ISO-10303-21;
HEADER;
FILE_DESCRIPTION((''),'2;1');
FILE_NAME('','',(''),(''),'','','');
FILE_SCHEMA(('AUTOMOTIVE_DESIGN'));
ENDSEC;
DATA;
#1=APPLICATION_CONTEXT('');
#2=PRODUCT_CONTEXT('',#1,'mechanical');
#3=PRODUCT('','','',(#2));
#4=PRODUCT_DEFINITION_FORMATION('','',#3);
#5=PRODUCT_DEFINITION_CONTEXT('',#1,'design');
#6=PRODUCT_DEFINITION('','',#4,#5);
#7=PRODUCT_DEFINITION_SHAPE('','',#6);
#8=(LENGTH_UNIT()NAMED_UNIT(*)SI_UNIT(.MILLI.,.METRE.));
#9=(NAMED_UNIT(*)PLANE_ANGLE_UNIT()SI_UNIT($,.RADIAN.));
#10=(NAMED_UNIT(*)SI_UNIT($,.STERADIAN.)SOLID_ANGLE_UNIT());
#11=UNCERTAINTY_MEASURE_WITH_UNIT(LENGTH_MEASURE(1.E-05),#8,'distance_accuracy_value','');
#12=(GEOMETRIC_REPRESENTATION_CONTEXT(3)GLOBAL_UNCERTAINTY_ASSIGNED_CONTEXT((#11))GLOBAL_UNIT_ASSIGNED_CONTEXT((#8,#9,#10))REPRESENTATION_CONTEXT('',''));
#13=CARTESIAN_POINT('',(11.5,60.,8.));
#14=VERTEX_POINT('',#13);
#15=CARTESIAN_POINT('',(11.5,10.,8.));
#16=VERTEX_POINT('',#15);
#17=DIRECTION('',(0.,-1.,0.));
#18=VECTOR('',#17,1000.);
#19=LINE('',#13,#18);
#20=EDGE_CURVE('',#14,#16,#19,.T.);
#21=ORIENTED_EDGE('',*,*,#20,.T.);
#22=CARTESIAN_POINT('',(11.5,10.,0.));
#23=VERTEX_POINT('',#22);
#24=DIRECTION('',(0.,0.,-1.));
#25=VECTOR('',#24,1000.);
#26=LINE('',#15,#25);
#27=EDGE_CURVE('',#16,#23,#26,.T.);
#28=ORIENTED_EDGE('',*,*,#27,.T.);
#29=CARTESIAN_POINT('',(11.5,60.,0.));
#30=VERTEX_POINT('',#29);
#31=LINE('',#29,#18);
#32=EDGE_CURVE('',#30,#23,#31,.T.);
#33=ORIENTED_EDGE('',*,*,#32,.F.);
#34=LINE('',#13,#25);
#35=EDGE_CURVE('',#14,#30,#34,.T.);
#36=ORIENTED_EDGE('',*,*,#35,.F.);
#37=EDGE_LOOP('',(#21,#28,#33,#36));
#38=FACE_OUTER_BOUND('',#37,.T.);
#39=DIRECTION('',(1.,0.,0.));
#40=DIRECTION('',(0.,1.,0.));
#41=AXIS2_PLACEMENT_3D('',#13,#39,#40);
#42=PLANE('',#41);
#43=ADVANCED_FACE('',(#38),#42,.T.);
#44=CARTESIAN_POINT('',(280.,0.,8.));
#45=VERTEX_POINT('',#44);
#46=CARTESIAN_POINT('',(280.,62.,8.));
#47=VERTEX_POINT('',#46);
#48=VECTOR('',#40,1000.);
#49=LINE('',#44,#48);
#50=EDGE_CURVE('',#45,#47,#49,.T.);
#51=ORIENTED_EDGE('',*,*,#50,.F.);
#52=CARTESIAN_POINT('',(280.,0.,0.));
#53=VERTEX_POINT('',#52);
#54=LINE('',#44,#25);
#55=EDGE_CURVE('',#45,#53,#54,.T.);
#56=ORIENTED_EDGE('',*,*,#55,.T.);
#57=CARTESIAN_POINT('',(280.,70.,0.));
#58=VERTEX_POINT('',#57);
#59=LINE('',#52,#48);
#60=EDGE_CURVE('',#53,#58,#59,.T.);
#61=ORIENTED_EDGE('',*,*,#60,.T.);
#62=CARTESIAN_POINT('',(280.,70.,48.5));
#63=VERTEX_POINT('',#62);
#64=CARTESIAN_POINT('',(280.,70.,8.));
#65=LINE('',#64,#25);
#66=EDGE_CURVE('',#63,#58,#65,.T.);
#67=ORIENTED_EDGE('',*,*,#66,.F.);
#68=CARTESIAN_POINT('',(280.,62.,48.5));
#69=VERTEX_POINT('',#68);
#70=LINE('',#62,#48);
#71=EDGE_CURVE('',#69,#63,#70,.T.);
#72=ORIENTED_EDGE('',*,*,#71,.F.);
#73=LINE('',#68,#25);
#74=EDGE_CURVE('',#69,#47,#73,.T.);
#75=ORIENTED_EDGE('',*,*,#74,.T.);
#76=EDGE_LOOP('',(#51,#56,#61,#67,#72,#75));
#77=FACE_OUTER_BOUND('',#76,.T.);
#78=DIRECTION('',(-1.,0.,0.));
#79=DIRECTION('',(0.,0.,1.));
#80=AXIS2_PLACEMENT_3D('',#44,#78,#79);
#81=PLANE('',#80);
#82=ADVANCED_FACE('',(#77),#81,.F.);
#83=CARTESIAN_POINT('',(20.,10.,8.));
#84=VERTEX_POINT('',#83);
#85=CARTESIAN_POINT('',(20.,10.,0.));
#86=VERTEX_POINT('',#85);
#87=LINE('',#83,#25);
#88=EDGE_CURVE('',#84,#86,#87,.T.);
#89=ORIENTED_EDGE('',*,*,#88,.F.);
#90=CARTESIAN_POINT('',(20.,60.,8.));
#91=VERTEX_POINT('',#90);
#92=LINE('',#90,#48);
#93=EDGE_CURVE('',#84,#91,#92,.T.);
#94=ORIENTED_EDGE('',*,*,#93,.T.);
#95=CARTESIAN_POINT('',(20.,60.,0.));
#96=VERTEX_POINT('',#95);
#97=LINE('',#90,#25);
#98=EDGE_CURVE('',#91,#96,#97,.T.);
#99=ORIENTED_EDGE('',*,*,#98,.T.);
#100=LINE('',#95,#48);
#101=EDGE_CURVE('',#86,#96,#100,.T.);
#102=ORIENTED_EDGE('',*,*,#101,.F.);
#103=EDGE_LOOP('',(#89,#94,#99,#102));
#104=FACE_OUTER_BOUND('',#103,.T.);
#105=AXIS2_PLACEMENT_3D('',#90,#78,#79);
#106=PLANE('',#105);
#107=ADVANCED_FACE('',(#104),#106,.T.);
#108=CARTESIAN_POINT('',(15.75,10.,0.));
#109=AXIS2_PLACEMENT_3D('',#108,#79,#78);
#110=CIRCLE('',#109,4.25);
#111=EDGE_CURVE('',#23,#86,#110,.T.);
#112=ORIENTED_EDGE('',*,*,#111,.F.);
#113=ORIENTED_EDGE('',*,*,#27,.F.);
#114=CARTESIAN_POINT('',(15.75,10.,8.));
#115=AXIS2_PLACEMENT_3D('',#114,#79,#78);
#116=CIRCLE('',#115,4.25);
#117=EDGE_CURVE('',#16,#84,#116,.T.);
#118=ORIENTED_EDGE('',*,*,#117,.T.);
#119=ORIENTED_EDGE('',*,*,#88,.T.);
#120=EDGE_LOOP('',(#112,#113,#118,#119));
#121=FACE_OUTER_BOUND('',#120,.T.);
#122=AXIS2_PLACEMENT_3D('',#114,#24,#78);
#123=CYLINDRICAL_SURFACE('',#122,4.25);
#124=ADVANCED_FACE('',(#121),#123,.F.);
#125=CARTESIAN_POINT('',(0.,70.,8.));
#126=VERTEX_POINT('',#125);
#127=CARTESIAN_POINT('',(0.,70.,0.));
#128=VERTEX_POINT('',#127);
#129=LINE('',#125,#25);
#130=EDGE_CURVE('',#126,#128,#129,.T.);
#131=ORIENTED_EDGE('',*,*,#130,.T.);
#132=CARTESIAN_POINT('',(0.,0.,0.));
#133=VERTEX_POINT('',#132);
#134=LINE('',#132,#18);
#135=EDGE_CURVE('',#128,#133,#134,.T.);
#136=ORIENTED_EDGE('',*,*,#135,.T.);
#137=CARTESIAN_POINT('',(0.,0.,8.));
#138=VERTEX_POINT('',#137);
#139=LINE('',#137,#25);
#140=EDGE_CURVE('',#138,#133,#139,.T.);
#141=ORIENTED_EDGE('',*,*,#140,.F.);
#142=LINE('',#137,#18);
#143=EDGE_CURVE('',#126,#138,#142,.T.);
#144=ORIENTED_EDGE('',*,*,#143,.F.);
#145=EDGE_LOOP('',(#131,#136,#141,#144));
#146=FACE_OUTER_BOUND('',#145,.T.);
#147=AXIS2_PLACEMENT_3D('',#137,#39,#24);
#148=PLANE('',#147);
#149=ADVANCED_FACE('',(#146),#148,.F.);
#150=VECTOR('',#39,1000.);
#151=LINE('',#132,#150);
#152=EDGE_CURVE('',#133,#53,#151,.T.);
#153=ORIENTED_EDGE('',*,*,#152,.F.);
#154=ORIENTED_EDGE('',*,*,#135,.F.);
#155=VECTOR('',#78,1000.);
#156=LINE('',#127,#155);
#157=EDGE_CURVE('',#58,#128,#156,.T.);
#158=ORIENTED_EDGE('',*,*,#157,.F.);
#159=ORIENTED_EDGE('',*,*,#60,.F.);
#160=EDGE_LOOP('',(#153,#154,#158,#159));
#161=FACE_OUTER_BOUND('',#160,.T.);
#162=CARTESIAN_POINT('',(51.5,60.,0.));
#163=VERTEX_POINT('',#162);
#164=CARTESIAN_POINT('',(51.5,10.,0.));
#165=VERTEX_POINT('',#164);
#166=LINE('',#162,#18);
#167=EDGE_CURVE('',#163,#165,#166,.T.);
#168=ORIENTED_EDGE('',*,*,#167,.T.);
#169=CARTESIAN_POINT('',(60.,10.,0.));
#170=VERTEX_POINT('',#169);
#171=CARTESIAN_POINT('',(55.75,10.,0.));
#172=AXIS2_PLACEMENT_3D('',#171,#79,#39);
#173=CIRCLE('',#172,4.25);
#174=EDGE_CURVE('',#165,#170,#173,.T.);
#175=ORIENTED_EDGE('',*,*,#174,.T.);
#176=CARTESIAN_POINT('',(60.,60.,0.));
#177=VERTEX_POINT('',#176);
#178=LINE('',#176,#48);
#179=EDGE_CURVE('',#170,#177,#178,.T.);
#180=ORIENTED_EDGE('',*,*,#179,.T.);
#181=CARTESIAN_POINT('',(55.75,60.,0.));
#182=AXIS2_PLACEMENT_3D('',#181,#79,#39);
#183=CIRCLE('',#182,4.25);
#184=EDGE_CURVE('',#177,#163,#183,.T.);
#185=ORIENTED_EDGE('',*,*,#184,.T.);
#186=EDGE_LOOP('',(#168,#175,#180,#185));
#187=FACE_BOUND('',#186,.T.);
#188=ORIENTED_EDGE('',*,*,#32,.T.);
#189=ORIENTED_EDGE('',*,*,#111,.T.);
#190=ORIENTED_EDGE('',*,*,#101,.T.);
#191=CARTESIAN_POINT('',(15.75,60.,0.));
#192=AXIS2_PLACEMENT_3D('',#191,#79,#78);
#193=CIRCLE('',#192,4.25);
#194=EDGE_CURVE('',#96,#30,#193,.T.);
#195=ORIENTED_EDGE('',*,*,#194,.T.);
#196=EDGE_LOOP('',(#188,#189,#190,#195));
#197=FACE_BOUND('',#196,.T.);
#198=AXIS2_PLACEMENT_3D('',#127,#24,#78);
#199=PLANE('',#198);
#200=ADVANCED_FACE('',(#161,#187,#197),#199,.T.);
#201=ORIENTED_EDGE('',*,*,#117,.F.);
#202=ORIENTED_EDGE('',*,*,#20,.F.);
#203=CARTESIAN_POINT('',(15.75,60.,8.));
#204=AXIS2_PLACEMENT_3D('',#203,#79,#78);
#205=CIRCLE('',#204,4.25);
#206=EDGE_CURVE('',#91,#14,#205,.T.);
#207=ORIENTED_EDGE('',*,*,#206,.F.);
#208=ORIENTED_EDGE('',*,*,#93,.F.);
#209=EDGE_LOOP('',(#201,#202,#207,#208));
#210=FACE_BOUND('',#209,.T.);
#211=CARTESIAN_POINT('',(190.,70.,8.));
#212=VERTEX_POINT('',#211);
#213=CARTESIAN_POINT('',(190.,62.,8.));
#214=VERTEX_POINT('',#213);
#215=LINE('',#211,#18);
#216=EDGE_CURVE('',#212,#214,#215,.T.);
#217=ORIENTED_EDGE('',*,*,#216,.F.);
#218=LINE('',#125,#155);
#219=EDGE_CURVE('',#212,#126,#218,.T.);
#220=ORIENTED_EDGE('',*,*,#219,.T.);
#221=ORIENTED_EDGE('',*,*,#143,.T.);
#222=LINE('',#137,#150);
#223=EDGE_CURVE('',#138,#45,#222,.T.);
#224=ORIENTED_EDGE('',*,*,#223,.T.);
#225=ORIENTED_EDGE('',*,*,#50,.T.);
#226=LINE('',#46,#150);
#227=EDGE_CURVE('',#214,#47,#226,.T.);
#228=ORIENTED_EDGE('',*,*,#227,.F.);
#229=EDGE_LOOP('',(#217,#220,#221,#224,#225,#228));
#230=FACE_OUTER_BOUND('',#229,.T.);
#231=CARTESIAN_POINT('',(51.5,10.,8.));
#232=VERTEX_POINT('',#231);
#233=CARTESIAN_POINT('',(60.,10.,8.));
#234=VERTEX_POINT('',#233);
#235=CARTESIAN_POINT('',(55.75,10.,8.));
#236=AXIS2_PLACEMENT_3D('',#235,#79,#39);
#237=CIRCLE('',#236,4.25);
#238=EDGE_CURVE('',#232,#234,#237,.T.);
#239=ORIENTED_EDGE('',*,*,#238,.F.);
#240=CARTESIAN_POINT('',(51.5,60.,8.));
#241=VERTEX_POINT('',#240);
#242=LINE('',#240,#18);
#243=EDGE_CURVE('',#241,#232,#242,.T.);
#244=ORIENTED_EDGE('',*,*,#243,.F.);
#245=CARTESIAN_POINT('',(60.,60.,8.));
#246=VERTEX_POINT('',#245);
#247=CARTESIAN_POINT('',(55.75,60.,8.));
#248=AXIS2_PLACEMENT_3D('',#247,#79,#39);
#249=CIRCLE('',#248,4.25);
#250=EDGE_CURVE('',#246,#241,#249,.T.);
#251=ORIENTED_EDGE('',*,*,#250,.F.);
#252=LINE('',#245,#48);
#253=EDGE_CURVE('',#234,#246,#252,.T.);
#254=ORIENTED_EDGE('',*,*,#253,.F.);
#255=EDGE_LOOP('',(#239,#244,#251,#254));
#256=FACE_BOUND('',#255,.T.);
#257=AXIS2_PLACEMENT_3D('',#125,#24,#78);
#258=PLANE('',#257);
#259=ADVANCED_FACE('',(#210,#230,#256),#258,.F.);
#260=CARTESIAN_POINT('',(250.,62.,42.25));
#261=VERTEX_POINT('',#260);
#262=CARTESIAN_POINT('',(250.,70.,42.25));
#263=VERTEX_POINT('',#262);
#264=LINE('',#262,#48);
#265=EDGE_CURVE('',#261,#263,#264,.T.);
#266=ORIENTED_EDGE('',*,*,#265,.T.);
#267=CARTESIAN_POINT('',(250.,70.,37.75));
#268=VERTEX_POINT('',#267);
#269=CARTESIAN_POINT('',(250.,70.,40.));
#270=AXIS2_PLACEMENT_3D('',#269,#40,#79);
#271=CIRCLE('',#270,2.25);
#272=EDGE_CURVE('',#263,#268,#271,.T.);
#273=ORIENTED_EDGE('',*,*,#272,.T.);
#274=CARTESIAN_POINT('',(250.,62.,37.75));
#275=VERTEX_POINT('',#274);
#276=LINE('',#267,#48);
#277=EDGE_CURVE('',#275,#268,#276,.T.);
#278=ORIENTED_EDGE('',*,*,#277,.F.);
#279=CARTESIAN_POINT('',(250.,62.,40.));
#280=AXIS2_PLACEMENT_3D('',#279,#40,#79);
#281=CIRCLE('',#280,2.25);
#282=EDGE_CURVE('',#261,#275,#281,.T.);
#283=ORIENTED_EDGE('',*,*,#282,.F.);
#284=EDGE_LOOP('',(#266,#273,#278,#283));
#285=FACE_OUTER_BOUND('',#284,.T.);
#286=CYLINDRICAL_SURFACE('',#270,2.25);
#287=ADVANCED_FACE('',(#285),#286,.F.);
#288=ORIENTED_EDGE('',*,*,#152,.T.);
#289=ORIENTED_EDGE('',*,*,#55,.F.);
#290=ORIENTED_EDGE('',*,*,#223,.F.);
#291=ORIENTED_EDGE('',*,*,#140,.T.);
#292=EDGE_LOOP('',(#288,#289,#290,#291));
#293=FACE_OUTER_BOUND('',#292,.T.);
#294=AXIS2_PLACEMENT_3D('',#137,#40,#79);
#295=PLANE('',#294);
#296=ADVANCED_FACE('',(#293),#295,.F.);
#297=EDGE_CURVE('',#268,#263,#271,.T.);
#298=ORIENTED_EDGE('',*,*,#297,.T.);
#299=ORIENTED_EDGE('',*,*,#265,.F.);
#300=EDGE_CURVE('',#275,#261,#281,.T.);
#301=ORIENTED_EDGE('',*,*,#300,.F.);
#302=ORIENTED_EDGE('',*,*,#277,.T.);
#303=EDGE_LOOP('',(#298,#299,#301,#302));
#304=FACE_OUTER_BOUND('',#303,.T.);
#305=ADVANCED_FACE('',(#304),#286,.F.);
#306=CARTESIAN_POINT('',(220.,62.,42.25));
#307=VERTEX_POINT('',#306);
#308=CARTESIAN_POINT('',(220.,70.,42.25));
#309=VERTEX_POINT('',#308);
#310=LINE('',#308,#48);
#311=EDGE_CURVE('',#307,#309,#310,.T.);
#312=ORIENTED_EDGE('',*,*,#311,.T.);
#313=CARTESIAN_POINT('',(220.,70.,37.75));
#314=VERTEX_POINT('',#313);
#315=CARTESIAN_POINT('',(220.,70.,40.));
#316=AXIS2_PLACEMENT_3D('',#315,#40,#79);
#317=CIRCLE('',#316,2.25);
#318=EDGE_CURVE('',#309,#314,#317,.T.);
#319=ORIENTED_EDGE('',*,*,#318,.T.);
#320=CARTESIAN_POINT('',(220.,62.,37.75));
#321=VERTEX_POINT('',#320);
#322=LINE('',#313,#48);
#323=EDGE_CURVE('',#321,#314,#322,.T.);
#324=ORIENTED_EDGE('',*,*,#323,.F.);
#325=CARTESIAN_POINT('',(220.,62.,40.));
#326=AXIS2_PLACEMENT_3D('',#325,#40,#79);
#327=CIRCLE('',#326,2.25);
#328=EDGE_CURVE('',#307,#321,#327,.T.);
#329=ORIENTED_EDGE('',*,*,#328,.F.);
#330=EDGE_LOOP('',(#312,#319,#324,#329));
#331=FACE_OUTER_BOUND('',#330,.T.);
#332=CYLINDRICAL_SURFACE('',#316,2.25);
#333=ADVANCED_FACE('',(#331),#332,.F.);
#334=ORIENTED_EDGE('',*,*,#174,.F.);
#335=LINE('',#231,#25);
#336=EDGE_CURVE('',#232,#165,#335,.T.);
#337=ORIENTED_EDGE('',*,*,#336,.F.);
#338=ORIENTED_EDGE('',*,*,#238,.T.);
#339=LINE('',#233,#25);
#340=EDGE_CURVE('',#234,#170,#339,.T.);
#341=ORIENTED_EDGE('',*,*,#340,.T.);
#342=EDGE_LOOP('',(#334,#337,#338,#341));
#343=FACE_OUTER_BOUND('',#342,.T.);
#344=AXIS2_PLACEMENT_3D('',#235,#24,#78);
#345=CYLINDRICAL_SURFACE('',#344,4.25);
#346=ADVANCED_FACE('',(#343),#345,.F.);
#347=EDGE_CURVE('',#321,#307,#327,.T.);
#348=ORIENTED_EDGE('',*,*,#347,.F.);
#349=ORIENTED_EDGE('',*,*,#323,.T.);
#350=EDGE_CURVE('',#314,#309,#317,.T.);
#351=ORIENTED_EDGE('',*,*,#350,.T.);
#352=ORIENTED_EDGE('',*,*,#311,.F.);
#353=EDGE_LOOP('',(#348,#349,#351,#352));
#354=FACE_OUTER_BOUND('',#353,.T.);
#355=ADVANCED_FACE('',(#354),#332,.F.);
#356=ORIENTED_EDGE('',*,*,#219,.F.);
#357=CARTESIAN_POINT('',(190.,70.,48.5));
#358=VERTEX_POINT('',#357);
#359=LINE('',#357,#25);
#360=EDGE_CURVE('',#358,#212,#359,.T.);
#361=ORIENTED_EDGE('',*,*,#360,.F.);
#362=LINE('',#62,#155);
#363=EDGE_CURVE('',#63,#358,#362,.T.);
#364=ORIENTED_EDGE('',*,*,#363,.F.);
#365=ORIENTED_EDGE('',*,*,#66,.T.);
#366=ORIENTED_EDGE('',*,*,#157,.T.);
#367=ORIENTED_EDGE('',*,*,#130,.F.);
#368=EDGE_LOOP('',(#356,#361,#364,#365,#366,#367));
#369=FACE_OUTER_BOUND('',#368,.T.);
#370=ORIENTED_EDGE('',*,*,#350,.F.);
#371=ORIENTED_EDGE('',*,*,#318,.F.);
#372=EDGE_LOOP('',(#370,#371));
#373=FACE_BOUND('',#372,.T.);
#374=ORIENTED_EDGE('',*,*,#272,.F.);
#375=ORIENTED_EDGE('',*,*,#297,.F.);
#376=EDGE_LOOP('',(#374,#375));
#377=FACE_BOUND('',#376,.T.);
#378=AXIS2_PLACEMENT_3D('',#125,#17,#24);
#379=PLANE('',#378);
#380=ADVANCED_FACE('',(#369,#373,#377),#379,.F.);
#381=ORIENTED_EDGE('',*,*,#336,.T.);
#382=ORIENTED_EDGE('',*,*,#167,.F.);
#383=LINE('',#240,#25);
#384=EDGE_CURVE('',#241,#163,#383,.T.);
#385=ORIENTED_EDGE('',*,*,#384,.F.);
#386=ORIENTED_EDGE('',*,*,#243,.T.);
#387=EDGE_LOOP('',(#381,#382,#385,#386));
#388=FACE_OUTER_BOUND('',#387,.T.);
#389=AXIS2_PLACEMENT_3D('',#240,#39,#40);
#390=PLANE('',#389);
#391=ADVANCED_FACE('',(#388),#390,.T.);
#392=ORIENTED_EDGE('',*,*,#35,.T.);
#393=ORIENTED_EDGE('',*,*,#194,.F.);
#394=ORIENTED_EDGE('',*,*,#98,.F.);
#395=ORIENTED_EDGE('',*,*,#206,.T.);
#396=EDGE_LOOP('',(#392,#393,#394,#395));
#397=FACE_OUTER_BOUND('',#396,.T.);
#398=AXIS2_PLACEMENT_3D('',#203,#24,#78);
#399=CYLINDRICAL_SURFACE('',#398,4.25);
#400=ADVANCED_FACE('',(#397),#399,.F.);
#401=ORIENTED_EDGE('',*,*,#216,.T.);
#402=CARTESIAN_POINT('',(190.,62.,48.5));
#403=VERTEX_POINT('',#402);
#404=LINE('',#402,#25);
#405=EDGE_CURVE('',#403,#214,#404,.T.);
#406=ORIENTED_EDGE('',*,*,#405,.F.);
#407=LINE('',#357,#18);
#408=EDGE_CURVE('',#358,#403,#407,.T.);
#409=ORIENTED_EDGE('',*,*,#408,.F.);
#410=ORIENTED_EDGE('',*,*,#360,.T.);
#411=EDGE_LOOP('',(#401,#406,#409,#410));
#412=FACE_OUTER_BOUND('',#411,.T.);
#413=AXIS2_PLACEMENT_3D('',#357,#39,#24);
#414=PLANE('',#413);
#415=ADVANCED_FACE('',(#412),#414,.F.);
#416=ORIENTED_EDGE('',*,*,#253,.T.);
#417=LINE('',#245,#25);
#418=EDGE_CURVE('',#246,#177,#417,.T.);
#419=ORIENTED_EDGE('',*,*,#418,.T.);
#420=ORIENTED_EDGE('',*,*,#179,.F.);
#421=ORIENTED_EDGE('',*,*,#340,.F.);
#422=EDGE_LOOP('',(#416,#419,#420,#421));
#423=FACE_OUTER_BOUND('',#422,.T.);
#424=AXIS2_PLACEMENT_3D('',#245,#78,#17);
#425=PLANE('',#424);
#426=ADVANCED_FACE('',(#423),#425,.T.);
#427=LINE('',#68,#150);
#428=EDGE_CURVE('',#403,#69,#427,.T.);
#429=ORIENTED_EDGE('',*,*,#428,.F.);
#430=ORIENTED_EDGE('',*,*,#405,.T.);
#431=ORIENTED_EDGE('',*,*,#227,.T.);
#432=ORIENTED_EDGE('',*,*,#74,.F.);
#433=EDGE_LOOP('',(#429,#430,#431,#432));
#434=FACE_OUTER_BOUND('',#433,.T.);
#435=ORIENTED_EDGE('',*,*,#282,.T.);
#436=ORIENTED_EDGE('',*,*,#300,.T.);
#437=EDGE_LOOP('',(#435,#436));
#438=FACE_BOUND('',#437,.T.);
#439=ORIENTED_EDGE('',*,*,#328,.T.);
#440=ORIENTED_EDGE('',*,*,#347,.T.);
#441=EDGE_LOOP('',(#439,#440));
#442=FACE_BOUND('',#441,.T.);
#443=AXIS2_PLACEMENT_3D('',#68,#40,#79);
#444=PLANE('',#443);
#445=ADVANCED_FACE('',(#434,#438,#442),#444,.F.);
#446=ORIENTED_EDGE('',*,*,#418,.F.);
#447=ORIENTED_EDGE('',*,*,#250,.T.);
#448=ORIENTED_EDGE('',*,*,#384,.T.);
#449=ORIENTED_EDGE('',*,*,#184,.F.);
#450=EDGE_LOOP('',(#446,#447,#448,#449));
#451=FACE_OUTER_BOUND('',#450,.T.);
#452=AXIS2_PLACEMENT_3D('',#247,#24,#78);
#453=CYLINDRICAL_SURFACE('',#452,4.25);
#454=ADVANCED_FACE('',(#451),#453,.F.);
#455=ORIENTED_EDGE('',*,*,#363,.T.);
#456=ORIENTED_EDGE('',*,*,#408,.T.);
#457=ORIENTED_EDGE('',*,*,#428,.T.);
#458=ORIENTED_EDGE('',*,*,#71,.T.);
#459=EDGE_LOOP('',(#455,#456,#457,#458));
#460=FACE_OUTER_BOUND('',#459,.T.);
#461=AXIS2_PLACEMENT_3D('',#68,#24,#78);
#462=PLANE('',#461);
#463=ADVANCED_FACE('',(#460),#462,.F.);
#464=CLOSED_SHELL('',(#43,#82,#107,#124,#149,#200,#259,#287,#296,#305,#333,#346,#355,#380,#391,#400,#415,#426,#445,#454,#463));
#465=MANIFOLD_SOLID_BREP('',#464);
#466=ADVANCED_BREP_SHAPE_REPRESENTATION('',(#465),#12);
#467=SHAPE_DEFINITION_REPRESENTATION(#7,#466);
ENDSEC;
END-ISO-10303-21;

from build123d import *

# Parameters (mm, degrees)
SKETCH_1_W              = 280
SKETCH_1_H              = 70
EXTRUDE_1_DEPTH         = 8
SKETCH_2_W              = 90
SKETCH_2_H              = 8
EXTRUDE_2_DEPTH         = 40.5
HOLE_WIZARD_4_5_4_5_1_D = 4.5


with BuildPart() as part:
    # 草图1 → 凸台-拉伸1 (new body)
    with BuildSketch(Plane.XY):
        with Locations((140, 35)):
            Rectangle(SKETCH_1_W, SKETCH_1_H)
        with BuildLine():
            Line((51.5, 60), (51.5, 10))
            ThreePointArc((51.5, 10), (55.75, 5.75), (60, 10))
            Line((60, 10), (60, 60))
            ThreePointArc((60, 60), (55.75, 64.25), (51.5, 60))
        make_face(mode=Mode.SUBTRACT)
        with BuildLine():
            Line((11.5, 60), (11.5, 10))
            ThreePointArc((11.5, 10), (15.75, 5.75), (20, 10))
            Line((20, 10), (20, 60))
            ThreePointArc((20, 60), (15.75, 64.25), (11.5, 60))
        make_face(mode=Mode.SUBTRACT)
    extrude(amount=EXTRUDE_1_DEPTH)

    # 草图2 → 凸台-拉伸2 (add)
    with BuildSketch(Plane.XY.offset(8)):
        with Locations((235, 66)):
            Rectangle(SKETCH_2_W, SKETCH_2_H)
    extrude(amount=EXTRUDE_2_DEPTH)

    # Ø4.5 (4.5) 直径孔1 (through all)
    with Locations(Plane(origin=(0, 70, 0), x_dir=(-1, 0, 0), z_dir=(0, 1, 0))):
        with Locations((-220, 40), (-250, 40)):
            Hole(HOLE_WIZARD_4_5_4_5_1_D / 2)


solid = part.part
